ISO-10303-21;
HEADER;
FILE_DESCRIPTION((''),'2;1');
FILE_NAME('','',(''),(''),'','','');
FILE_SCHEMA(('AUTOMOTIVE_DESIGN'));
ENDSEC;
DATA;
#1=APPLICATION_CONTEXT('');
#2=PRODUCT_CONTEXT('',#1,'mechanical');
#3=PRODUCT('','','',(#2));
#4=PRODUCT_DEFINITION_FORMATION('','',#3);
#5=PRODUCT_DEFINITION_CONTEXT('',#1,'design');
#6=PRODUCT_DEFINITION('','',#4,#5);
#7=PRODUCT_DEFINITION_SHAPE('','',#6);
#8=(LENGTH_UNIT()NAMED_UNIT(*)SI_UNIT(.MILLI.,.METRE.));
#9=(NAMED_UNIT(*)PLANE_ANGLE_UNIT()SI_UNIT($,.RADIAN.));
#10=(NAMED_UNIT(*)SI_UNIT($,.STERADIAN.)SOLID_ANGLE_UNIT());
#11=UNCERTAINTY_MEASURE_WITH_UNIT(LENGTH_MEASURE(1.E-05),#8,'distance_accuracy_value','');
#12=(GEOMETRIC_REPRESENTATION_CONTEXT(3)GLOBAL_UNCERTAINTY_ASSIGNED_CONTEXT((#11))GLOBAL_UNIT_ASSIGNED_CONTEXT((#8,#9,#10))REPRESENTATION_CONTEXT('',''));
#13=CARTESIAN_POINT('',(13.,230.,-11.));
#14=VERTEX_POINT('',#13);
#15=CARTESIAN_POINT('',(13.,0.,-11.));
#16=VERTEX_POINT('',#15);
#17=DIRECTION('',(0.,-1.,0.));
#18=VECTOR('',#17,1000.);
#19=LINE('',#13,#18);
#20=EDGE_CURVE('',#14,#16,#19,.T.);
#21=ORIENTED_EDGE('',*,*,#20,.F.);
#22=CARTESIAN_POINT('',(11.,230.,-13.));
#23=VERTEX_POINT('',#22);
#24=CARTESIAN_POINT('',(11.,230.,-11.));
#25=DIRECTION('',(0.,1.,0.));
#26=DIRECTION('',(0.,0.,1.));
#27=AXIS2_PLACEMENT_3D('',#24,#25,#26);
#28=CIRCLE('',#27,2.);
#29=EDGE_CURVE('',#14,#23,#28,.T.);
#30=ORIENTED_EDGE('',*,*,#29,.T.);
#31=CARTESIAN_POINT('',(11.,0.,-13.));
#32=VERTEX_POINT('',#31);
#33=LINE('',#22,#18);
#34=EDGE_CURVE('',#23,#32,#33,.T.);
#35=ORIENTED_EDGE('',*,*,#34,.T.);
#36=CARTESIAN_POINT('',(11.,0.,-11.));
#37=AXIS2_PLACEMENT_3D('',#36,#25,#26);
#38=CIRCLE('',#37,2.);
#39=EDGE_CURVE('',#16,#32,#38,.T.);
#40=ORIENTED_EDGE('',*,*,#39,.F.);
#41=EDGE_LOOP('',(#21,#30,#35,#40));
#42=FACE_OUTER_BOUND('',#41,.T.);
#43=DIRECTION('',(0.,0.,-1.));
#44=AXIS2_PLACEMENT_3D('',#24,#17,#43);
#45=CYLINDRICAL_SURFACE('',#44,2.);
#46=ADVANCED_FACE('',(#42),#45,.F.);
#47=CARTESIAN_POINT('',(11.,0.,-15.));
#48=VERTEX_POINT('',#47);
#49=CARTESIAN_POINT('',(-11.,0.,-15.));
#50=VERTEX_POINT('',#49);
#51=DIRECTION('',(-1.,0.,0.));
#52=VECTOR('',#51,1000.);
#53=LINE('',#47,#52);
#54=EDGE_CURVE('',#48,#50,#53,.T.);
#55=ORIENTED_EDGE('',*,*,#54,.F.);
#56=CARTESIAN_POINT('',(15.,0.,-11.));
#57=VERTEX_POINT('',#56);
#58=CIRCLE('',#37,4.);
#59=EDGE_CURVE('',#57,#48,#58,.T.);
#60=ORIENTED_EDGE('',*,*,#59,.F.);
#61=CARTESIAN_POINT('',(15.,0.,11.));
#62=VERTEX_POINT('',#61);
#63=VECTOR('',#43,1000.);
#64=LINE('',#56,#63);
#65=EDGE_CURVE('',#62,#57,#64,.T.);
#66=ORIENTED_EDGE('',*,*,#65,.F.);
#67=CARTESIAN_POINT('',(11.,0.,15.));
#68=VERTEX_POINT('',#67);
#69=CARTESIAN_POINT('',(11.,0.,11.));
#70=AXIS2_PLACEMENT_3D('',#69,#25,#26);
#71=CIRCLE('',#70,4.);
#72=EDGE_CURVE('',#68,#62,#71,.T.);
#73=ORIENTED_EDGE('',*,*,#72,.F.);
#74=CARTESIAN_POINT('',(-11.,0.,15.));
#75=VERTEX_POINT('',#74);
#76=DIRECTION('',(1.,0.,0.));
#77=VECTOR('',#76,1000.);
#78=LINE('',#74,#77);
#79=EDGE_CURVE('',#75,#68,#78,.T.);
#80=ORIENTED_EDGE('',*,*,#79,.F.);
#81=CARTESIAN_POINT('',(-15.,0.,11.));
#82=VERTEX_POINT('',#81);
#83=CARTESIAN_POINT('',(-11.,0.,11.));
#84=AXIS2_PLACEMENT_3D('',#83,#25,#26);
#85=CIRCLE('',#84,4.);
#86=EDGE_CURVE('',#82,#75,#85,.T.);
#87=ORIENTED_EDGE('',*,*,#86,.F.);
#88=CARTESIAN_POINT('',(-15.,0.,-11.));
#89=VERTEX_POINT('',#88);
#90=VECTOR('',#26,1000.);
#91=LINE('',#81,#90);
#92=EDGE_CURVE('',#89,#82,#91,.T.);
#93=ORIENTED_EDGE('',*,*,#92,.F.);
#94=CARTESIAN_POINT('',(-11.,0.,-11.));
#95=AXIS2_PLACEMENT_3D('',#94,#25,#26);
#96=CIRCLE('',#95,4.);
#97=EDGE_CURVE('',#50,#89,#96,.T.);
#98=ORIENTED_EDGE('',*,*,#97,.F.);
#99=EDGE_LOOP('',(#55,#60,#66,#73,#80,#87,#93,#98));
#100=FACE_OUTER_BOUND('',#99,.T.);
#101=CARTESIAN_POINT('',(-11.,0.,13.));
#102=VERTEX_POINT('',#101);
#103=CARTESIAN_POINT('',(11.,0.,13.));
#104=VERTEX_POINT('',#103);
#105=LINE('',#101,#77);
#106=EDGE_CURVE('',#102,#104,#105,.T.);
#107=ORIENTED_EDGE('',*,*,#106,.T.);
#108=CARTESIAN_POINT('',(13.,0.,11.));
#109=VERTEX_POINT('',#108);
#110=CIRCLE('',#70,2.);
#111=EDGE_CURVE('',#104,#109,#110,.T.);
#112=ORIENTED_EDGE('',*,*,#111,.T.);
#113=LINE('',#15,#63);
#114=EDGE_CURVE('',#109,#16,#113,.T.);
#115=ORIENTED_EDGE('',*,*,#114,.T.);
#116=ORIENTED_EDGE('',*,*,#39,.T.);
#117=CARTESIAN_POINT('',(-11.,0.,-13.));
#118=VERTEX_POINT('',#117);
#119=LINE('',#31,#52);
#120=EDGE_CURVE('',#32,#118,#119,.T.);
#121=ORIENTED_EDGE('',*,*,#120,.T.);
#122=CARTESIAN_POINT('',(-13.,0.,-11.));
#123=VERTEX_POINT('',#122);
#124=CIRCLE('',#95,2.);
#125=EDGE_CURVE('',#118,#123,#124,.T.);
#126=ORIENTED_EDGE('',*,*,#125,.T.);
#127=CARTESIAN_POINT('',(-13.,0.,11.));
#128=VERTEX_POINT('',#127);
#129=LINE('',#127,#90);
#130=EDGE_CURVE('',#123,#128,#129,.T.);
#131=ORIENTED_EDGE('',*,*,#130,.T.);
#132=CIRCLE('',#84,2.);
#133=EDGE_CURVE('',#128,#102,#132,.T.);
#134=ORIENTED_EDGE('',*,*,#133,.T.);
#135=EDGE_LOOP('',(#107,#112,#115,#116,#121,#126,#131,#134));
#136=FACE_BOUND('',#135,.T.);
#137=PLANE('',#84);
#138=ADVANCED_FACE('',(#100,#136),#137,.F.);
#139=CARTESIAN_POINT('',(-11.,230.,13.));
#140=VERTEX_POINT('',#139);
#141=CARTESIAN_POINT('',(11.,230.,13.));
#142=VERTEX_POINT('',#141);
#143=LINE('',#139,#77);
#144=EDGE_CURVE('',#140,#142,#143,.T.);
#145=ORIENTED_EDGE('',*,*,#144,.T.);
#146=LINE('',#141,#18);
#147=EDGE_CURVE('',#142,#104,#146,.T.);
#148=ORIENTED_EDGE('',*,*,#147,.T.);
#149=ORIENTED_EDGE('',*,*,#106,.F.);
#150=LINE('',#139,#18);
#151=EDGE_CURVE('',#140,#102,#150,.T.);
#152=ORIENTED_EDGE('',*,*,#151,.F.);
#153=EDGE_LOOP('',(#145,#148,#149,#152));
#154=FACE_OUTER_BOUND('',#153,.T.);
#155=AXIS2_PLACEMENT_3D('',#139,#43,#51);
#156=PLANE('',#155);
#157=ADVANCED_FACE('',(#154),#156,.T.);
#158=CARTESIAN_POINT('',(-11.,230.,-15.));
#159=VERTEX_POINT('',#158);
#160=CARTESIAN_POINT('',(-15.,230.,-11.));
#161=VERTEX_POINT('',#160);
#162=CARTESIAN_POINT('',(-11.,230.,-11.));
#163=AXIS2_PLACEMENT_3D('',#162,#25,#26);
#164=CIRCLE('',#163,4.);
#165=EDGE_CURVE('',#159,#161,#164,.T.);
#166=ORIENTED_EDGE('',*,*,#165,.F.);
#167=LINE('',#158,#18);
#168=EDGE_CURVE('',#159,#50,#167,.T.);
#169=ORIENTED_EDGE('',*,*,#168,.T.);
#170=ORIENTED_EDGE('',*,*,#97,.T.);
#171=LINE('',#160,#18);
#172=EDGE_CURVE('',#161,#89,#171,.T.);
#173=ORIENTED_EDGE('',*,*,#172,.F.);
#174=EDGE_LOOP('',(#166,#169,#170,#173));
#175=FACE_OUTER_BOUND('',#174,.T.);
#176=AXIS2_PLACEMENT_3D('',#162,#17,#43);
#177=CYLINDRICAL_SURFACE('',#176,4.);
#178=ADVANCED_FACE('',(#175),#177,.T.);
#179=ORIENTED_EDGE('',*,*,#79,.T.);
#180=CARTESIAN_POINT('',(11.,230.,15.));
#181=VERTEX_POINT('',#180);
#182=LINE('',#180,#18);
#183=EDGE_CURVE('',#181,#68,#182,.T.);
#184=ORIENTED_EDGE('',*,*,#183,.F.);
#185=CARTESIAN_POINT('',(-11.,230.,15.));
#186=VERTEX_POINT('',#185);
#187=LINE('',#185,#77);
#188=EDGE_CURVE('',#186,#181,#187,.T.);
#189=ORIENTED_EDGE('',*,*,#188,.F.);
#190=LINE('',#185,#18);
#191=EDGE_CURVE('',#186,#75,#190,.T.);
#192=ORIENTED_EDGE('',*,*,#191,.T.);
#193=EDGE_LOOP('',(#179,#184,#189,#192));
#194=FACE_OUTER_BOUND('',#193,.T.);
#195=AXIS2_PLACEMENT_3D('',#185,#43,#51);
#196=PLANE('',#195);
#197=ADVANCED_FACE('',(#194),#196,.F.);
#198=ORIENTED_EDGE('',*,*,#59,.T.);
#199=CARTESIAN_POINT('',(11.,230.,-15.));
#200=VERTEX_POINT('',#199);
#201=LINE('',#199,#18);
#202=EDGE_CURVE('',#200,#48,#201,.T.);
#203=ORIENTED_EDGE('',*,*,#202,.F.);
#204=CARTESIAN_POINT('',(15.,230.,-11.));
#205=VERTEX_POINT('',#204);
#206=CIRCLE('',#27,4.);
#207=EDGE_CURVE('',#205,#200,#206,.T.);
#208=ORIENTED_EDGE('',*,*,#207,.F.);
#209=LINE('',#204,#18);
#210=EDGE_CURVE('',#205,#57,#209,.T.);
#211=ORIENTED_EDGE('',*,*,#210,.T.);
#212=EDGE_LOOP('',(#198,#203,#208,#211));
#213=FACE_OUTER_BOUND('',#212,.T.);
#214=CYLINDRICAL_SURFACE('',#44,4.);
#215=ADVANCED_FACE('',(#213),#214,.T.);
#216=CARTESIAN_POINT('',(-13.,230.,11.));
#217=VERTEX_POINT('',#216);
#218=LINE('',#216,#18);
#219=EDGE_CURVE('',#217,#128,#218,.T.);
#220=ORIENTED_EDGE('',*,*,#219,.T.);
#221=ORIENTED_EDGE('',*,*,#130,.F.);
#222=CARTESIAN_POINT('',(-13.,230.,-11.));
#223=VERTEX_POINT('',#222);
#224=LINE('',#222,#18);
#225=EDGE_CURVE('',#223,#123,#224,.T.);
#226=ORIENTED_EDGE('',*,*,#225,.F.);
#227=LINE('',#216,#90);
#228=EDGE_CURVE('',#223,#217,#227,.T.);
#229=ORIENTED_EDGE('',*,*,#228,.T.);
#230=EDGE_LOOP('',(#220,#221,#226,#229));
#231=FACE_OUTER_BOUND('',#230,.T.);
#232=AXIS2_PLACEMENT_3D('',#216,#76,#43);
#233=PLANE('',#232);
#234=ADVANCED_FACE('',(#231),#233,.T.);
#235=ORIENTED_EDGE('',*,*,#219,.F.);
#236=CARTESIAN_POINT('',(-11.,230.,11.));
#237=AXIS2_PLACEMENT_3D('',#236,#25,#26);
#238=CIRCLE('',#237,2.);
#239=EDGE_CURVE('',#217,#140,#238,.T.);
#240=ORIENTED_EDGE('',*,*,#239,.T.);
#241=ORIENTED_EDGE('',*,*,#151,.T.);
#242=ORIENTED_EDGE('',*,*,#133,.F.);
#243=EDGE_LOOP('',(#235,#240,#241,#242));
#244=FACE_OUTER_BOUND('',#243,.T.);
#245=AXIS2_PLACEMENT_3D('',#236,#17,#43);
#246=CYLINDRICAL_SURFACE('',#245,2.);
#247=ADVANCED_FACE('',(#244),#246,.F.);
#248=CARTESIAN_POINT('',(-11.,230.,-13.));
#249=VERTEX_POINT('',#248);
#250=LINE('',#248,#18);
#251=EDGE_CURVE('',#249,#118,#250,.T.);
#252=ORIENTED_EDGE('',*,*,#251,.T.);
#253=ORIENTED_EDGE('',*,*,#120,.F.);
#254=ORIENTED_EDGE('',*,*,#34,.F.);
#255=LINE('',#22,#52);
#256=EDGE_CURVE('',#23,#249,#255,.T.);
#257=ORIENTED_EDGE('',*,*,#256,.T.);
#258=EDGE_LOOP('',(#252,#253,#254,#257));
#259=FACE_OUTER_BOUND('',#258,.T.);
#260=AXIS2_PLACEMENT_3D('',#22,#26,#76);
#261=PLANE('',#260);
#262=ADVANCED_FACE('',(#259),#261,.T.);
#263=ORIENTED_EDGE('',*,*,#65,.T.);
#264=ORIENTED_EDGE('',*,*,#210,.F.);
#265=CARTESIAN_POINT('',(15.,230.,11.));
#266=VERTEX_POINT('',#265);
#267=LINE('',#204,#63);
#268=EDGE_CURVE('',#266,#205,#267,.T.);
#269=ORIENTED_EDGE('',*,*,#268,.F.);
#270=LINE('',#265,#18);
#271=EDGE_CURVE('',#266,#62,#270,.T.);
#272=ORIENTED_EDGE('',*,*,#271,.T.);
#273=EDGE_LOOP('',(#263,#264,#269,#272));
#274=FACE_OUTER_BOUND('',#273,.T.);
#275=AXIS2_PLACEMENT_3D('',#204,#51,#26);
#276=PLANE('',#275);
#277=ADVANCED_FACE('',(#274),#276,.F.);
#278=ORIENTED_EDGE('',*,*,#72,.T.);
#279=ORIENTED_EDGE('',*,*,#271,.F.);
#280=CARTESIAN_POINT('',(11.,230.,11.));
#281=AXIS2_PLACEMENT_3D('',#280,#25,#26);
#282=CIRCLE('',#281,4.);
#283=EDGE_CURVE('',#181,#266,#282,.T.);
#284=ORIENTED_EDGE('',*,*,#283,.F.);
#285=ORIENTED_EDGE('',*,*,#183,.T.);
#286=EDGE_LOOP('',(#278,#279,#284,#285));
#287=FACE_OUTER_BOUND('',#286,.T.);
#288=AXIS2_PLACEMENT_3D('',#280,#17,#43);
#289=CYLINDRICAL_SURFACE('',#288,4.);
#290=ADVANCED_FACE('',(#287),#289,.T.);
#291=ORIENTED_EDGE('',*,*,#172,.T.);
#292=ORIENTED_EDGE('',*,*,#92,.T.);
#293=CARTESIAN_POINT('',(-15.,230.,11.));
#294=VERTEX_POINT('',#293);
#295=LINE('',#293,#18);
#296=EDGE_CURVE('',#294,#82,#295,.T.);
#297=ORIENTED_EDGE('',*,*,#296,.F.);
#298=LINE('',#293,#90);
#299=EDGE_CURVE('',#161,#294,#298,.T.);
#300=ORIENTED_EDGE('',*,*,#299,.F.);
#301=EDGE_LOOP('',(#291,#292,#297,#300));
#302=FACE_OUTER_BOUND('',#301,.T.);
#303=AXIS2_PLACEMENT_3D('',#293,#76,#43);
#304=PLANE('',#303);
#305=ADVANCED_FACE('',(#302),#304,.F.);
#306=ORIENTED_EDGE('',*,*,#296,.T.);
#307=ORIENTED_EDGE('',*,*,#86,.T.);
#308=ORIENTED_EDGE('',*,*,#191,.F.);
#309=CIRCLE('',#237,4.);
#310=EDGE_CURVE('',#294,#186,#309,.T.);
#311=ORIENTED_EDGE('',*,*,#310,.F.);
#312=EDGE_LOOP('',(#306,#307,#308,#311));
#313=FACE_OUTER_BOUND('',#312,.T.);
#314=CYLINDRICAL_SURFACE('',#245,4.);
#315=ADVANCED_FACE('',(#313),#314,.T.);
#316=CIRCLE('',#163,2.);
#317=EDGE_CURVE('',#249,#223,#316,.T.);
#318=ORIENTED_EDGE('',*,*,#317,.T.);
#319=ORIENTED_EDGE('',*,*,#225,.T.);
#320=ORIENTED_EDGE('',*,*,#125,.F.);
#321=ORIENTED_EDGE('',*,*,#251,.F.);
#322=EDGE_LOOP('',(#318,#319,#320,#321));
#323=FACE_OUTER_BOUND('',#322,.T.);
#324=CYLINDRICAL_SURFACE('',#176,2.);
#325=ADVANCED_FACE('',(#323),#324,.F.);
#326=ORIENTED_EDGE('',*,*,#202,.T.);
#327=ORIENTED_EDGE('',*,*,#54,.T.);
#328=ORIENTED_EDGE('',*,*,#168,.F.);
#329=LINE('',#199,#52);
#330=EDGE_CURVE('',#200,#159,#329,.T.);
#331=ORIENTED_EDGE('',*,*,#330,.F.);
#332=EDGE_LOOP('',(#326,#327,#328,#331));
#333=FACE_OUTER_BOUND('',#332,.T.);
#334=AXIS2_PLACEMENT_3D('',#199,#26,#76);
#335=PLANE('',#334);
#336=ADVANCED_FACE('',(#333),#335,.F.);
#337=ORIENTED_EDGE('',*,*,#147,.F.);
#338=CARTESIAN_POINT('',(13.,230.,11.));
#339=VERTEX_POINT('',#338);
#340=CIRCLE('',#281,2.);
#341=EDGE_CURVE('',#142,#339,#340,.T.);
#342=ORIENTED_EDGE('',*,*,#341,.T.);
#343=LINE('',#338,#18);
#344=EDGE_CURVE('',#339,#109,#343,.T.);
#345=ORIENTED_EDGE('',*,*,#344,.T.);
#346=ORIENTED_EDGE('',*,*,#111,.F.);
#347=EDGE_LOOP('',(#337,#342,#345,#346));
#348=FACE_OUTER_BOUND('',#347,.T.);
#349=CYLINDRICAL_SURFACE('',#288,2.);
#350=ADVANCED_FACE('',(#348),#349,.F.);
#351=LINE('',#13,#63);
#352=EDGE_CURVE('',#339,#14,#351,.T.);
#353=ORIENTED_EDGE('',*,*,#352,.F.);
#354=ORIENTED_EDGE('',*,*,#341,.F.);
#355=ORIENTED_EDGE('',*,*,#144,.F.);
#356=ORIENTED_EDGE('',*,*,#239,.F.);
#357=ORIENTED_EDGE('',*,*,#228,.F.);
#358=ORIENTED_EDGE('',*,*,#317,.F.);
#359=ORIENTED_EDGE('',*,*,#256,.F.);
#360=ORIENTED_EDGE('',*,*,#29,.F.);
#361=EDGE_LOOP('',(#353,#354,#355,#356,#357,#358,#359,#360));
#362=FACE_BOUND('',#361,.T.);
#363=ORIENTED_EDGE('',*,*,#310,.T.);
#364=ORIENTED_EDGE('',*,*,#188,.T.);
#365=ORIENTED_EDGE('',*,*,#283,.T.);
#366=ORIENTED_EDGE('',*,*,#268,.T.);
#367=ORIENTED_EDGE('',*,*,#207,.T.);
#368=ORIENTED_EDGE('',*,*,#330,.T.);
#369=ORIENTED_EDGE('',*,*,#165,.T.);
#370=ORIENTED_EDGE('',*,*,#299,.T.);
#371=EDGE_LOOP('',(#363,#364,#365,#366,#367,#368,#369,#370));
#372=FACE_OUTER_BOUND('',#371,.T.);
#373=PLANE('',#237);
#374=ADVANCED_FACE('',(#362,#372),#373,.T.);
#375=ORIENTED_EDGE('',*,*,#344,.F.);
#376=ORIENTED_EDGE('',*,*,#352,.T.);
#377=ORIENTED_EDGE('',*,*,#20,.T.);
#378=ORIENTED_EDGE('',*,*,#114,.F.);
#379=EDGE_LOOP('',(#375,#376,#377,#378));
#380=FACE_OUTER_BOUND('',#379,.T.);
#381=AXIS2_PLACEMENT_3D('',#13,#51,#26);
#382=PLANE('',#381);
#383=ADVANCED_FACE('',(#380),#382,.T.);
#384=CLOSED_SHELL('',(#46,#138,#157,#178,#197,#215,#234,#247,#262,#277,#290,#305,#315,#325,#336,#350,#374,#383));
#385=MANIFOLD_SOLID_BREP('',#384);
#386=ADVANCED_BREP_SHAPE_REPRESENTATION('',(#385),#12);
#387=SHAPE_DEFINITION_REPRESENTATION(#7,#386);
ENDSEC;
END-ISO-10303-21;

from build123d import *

# Parameters (mm, degrees)
GB_T_6728_2002_SQUARE_HOLLOW_SECTION_30_DEPTH = 230


with BuildPart() as part:
    # Sketch11 → Gb／t 6728—2002 square hollow section 30×30×2(1) (new body)
    with BuildSketch(Plane(origin=(0, 0, 0), x_dir=(-1, 0, 0), z_dir=(0, 1, 0))):
        with BuildLine():
            Line((-11, -15), (11, -15))
            ThreePointArc((11, -15), (13.828427125, -13.828427125), (15, -11))
            Line((15, -11), (15, 11))
            ThreePointArc((15, 11), (13.828427125, 13.828427125), (11, 15))
            Line((11, 15), (-11, 15))
            ThreePointArc((-11, 15), (-13.828427125, 13.828427125), (-15, 11))
            Line((-15, 11), (-15, -11))
            ThreePointArc((-15, -11), (-13.828427125, -13.828427125), (-11, -15))
        make_face()
        with BuildLine():
            Line((-11, -13), (11, -13))
            ThreePointArc((11, -13), (12.414213562, -12.414213562), (13, -11))
            Line((13, -11), (13, 11))
            ThreePointArc((13, 11), (12.414213562, 12.414213562), (11, 13))
            Line((11, 13), (-11, 13))
            ThreePointArc((-11, 13), (-12.414213562, 12.414213562), (-13, 11))
            Line((-13, 11), (-13, -11))
            ThreePointArc((-13, -11), (-12.414213562, -12.414213562), (-11, -13))
        make_face(mode=Mode.SUBTRACT)
    extrude(amount=GB_T_6728_2002_SQUARE_HOLLOW_SECTION_30_DEPTH)


solid = part.part
